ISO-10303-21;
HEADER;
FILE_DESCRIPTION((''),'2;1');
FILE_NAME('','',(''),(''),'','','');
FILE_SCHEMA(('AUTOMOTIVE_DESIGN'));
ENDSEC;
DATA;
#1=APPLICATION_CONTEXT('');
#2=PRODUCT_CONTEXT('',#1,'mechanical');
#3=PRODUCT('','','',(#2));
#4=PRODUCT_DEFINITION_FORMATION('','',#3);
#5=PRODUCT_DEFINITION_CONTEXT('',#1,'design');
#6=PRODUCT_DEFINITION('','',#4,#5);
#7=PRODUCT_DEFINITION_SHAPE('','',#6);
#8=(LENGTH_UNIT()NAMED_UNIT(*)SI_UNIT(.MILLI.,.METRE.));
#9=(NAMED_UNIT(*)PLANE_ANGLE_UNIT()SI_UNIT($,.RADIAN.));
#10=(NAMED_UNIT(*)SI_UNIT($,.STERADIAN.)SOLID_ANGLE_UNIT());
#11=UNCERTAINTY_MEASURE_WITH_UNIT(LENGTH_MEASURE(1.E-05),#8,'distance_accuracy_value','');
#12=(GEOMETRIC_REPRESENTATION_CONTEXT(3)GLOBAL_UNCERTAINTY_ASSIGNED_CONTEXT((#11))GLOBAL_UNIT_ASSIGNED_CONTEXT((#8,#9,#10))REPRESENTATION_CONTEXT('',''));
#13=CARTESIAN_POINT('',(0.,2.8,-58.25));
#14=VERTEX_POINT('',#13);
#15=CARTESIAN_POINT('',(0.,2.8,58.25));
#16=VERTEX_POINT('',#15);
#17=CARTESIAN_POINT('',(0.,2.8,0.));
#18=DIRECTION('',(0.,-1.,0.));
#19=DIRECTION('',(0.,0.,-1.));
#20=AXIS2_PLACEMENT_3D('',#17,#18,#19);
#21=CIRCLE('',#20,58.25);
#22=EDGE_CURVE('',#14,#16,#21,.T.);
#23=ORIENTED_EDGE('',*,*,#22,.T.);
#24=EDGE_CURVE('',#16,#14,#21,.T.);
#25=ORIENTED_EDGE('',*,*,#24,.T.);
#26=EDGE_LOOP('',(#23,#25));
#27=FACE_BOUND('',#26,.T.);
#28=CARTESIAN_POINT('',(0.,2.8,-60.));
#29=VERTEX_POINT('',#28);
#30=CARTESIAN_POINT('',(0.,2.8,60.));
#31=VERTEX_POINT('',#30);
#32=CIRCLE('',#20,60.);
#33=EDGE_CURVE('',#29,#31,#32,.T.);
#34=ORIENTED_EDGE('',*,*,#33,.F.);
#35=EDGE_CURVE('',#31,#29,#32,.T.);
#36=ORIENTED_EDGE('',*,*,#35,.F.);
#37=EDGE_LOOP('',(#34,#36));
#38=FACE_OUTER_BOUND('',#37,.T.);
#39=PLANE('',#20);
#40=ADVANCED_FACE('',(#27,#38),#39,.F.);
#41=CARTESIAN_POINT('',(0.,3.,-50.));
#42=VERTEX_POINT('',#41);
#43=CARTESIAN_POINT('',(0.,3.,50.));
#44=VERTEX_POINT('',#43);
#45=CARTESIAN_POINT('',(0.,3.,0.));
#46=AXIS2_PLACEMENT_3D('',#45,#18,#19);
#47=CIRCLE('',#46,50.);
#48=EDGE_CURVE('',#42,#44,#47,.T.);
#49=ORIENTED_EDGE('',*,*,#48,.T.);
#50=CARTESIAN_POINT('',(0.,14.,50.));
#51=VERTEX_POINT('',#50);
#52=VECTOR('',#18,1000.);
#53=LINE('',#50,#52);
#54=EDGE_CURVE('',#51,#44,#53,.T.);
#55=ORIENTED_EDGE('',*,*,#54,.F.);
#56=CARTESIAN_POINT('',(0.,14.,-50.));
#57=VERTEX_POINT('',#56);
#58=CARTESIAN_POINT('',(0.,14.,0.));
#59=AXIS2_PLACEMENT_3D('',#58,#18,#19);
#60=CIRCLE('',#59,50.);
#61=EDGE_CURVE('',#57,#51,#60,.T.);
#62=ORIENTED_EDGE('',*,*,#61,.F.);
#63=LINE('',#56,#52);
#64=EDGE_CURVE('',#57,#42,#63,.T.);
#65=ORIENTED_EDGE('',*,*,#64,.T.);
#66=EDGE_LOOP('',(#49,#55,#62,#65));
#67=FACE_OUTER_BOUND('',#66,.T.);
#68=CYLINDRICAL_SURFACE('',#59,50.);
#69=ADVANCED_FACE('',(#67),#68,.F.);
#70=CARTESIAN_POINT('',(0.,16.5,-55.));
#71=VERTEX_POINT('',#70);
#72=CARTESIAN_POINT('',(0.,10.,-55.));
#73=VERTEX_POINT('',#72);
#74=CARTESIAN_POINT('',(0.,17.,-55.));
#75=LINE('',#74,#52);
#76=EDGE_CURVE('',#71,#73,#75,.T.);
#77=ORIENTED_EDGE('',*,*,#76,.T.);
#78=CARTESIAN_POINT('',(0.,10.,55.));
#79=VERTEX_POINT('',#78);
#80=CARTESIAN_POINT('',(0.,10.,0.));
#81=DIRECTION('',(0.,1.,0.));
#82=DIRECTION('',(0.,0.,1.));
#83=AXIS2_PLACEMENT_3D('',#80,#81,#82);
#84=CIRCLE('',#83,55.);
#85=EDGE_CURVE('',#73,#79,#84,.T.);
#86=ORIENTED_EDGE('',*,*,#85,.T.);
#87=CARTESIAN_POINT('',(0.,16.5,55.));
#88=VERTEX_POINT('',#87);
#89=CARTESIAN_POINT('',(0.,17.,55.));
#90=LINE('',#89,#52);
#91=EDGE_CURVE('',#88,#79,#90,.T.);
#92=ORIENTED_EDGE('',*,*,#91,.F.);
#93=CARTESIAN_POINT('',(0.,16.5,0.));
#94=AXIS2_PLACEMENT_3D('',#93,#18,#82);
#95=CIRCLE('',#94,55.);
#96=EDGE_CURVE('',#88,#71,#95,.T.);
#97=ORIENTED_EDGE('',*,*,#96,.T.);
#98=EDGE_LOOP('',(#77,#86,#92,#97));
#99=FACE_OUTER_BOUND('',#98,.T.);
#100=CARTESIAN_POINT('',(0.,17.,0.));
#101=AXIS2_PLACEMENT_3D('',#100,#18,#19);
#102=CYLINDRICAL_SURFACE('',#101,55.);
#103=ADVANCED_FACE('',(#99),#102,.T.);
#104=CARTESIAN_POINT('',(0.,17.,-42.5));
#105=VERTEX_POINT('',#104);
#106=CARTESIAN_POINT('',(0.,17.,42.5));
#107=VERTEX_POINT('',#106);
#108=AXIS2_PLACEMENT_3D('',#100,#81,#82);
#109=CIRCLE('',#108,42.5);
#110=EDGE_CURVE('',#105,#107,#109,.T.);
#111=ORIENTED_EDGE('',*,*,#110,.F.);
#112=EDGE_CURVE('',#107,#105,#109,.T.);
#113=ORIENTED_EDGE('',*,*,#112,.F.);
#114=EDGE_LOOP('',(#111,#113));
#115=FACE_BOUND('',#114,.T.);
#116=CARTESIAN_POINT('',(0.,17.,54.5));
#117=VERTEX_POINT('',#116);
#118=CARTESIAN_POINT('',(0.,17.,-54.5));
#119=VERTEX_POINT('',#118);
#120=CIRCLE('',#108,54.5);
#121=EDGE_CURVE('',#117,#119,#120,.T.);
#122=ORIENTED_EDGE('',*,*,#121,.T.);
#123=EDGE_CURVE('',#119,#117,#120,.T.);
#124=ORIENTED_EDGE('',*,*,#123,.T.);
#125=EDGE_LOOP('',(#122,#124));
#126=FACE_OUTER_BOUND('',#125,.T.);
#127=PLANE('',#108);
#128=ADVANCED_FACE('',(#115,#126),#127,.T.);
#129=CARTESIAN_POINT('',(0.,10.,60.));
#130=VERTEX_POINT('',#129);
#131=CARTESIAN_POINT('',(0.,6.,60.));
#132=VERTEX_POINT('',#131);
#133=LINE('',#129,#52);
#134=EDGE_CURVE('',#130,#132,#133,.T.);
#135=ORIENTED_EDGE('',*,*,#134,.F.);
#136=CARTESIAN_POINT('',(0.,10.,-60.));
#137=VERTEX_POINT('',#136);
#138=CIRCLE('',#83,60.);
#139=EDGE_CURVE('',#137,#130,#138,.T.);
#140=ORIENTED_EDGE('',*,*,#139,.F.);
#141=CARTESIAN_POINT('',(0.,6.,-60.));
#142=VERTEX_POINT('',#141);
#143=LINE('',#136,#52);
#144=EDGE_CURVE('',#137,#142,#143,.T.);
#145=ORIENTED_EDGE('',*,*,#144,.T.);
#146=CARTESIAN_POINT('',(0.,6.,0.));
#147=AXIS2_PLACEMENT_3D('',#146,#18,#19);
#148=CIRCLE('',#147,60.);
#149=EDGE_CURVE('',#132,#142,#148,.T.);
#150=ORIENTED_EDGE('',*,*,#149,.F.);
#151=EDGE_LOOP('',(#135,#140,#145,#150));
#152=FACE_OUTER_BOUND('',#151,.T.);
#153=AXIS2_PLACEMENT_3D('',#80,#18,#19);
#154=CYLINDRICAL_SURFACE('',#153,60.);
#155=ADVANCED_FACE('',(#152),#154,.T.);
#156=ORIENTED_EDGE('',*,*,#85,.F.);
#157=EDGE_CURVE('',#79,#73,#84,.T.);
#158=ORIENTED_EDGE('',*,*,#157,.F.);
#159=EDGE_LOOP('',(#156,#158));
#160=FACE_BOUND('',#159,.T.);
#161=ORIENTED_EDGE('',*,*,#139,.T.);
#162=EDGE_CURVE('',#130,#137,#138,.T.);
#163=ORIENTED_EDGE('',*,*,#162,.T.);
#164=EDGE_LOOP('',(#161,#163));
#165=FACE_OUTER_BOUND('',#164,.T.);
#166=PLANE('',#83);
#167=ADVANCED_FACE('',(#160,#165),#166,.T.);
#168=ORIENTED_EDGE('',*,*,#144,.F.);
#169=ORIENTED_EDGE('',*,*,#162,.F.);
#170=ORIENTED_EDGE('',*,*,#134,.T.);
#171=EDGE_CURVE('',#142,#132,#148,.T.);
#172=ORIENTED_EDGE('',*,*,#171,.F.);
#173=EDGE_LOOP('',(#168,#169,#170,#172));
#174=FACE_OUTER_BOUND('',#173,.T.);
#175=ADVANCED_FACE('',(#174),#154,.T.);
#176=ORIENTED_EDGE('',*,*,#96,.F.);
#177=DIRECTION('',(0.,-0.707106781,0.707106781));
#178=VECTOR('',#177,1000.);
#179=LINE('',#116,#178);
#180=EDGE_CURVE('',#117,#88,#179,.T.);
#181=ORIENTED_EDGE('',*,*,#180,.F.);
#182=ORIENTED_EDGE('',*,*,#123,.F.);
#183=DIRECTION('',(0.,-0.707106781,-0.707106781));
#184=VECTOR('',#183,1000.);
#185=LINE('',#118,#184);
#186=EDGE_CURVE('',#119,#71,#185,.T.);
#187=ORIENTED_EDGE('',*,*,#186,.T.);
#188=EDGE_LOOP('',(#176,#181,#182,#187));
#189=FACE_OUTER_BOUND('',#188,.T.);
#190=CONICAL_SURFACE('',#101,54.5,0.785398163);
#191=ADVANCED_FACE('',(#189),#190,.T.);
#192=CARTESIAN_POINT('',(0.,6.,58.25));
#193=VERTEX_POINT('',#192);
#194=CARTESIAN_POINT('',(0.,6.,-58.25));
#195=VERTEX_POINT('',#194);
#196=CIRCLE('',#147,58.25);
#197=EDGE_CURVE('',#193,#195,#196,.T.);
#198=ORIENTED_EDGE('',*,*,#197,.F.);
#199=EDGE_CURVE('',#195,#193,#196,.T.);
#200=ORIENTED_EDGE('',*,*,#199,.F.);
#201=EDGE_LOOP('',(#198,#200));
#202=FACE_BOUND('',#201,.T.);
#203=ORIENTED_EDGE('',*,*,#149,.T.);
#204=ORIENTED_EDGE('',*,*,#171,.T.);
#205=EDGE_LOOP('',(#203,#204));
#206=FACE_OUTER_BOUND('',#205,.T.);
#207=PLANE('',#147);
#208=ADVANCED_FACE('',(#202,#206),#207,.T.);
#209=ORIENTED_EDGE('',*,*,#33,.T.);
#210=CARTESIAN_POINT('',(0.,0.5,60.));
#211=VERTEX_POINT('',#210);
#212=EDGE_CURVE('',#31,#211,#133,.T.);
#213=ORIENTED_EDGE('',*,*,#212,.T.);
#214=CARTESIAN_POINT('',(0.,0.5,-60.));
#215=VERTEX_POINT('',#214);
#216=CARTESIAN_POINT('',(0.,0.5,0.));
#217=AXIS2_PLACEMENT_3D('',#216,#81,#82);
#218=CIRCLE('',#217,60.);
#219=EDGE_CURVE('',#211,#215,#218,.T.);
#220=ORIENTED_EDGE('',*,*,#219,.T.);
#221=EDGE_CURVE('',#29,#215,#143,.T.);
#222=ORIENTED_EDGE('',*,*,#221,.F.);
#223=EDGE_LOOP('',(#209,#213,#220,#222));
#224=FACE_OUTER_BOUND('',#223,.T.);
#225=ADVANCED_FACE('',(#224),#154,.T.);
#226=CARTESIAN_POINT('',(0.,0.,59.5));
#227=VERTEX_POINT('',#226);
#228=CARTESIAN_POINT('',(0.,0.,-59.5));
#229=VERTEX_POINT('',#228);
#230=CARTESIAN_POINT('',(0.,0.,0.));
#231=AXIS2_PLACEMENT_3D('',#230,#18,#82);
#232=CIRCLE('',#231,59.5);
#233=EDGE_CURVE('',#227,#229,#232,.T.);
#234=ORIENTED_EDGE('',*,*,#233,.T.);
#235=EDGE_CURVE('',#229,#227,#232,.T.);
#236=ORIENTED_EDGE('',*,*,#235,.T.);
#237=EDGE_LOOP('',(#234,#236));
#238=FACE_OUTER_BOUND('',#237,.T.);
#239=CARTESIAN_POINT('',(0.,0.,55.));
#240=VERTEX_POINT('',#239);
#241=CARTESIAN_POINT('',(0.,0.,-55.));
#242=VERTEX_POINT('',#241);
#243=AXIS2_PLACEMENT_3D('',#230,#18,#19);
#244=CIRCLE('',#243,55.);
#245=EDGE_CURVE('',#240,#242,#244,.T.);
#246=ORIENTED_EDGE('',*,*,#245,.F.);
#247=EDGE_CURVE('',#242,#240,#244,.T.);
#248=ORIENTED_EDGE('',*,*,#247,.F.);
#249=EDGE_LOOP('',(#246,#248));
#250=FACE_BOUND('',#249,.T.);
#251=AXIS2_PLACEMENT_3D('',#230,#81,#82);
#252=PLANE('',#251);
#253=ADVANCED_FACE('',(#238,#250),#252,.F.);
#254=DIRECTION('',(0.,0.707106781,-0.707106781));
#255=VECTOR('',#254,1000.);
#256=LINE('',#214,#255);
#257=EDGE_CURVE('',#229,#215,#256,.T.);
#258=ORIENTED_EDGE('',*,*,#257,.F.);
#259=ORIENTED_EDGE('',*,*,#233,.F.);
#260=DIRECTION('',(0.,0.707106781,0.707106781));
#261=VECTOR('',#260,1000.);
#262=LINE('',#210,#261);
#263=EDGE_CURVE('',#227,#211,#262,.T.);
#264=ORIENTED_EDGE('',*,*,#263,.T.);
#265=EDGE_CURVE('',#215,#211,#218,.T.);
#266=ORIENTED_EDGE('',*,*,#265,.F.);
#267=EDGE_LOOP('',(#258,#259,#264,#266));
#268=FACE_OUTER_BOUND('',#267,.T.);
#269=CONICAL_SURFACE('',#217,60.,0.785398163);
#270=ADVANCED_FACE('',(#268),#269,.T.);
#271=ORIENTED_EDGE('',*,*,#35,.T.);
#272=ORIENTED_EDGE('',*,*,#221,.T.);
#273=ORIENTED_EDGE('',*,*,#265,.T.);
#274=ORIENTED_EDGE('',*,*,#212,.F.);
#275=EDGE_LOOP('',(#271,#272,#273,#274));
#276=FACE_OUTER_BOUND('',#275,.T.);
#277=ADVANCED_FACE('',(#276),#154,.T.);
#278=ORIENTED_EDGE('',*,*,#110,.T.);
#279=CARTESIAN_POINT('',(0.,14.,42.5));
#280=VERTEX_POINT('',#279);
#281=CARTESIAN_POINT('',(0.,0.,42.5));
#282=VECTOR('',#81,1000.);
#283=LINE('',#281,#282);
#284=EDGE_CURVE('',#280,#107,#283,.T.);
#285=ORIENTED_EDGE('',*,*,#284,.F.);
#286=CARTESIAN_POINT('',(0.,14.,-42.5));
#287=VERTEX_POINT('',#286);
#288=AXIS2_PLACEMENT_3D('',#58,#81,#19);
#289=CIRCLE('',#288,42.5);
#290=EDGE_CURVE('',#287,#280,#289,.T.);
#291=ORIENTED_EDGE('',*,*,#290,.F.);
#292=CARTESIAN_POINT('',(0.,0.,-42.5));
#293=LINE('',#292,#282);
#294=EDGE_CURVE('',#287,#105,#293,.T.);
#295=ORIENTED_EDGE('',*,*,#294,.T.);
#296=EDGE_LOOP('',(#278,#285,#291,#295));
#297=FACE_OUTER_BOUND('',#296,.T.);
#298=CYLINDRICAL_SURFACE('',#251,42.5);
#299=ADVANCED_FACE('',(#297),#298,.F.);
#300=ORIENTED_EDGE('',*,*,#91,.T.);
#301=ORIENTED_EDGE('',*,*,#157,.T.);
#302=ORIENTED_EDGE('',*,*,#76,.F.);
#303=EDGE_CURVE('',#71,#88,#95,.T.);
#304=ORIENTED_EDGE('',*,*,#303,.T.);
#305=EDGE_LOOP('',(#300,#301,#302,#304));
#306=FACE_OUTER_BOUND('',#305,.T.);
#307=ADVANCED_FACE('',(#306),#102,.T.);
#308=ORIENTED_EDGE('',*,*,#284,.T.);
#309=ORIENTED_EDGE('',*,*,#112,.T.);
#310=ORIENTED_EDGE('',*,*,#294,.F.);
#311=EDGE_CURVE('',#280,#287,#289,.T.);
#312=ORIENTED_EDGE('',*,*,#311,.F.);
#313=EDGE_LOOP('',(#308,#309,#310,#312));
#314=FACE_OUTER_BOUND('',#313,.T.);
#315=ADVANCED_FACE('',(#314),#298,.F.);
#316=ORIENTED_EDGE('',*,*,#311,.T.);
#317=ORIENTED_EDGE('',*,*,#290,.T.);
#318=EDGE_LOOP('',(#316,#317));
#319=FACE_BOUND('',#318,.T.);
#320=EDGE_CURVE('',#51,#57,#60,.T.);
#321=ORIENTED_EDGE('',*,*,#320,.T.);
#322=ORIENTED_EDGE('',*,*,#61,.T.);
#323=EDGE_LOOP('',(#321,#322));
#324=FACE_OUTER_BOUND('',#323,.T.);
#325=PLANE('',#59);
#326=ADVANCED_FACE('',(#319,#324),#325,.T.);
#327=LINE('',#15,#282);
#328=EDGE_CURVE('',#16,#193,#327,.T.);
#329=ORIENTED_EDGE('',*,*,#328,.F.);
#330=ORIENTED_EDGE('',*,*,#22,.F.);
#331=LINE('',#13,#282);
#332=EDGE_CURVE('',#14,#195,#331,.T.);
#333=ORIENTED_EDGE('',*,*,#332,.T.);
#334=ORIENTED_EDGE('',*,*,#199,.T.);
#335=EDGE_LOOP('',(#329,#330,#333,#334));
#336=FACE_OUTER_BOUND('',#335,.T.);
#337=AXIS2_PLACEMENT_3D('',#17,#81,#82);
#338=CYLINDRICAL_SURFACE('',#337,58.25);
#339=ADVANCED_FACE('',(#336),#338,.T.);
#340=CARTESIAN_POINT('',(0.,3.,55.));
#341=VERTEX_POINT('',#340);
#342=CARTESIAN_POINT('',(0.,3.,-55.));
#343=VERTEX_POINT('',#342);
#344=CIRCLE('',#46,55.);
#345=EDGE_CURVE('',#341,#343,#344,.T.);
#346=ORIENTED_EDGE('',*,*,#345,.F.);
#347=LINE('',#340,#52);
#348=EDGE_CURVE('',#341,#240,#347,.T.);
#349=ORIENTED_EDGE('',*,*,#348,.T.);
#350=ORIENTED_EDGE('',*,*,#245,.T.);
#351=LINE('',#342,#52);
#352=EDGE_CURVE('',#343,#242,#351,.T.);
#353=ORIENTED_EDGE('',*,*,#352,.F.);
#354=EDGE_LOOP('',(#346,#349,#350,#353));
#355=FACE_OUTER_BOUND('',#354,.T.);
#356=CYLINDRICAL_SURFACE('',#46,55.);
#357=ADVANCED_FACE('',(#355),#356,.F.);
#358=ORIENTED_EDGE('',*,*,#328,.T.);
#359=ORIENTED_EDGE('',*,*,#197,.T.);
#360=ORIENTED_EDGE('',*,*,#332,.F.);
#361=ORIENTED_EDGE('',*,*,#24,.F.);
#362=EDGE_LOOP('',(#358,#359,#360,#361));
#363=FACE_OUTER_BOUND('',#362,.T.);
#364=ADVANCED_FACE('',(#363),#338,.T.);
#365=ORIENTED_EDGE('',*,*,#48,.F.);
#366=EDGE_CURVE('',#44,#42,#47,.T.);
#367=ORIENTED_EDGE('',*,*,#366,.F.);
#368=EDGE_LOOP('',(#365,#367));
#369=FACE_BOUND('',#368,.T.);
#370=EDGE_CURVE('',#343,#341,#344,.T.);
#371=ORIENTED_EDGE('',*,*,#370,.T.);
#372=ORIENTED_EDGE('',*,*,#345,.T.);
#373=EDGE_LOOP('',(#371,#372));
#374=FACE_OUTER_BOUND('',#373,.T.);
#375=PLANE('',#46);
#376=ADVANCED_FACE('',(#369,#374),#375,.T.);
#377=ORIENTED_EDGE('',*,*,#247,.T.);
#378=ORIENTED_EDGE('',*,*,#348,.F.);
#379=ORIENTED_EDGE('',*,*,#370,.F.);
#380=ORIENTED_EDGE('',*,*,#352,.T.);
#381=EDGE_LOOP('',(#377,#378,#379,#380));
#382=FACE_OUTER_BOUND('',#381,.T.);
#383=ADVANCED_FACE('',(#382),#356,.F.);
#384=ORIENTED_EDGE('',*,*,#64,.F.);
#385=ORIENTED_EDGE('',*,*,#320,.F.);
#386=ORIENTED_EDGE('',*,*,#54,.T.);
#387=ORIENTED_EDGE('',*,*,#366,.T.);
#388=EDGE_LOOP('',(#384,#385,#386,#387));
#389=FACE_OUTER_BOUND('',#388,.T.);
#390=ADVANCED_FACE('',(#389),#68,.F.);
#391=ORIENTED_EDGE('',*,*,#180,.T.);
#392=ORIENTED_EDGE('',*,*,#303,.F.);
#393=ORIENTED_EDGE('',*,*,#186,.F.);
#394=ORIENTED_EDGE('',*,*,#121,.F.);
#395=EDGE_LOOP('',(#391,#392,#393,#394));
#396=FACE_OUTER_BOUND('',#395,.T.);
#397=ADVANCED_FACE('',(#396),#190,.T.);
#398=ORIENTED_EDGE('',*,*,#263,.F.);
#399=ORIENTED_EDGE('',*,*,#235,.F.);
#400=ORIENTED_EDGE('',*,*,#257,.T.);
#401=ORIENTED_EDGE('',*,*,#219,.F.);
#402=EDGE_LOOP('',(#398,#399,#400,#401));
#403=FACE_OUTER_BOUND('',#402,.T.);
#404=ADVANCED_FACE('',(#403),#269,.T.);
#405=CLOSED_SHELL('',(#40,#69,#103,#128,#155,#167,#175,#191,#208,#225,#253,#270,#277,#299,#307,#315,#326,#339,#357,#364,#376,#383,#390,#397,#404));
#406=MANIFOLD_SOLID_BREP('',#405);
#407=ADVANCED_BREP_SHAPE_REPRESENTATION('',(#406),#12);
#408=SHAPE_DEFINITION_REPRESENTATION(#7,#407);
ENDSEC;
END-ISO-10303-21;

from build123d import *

# Parameters (mm, degrees)
SKETCH1_R           = 60
BOSS_EXTRUDE1_DEPTH = 10
SKETCH2_R           = 55
BOSS_EXTRUDE2_DEPTH = 7
SKETCH3_R           = 42.5
CUT_EXTRUDE1_DEPTH  = 87.539008545
SKETCH4_R           = 55
CUT_EXTRUDE2_DEPTH  = 3
SKETCH5_R           = 50
CUT_EXTRUDE3_DEPTH  = 11
SKETCH6_OUTSIDE_W   = 156.11
SKETCH6_OUTSIDE_H   = 156.11
SKETCH6_OUTSIDE_R   = 58.25
CUT_EXTRUDE4_DEPTH  = 3.2
CHAMFER1_SIZE       = 0.5
CHAMFER2_SIZE       = 0.5


with BuildPart() as part:
    # Sketch1 → Boss-Extrude1 (new body)
    with BuildSketch(Plane(origin=(0, 0, 0), x_dir=(1, 0, 0), z_dir=(0, 1, 0))):
        with Locations(Location((0, 0, 0), (0, 0, 270))):
            Circle(SKETCH1_R)
    extrude(amount=BOSS_EXTRUDE1_DEPTH)

    # Sketch2 → Boss-Extrude2 (add)
    with BuildSketch(Plane(origin=(0, 10, 0), x_dir=(1, 0, 0), z_dir=(0, 1, 0))):
        with Locations(Location((0, 0, 0), (0, 0, 270))):
            Circle(SKETCH2_R)
    extrude(amount=BOSS_EXTRUDE2_DEPTH)

    # Sketch3 → Cut-Extrude1 (cut, through all)
    with BuildSketch(Plane(origin=(0, 17, 0), x_dir=(1, 0, 0), z_dir=(0, 1, 0))):
        with Locations(Location((0, 0, 0), (0, 0, 270))):
            Circle(SKETCH3_R)
    extrude(amount=-CUT_EXTRUDE1_DEPTH, mode=Mode.SUBTRACT)

    # Sketch4 → Cut-Extrude2 (cut)
    with BuildSketch(Plane.XZ):
        with Locations(Location((0, 0, 0), (0, 0, 90))):
            Circle(SKETCH4_R)
    extrude(amount=-CUT_EXTRUDE2_DEPTH, mode=Mode.SUBTRACT)

    # Sketch5 → Cut-Extrude3 (cut)
    with BuildSketch(Plane.XZ.offset(-3)):
        with Locations(Location((0, 0, 0), (0, 0, 270))):
            Circle(SKETCH5_R)
    extrude(amount=-CUT_EXTRUDE3_DEPTH, mode=Mode.SUBTRACT)

    # Sketch6 outside → Cut-Extrude4 (cut)
    with BuildSketch(Plane(origin=(0, 6, 0), x_dir=(-1, 0, 0), z_dir=(0, -1, 0))):
        Rectangle(SKETCH6_OUTSIDE_W, SKETCH6_OUTSIDE_H)
        with Locations(Location((0, 0, 0), (0, 0, 90))):
            Circle(SKETCH6_OUTSIDE_R, mode=Mode.SUBTRACT)
    extrude(amount=CUT_EXTRUDE4_DEPTH, mode=Mode.SUBTRACT)

    # Chamfer1
    chamfer1_edges = [part.edges().sort_by_distance(p)[0] for p in [
        (0, 0, -60),
    ]]
    chamfer(chamfer1_edges, length=CHAMFER1_SIZE)

    # Chamfer2
    chamfer2_edges = [part.edges().sort_by_distance(p)[0] for p in [
        (0, 17, -55),
    ]]
    chamfer(chamfer2_edges, length=CHAMFER2_SIZE)


solid = part.part
